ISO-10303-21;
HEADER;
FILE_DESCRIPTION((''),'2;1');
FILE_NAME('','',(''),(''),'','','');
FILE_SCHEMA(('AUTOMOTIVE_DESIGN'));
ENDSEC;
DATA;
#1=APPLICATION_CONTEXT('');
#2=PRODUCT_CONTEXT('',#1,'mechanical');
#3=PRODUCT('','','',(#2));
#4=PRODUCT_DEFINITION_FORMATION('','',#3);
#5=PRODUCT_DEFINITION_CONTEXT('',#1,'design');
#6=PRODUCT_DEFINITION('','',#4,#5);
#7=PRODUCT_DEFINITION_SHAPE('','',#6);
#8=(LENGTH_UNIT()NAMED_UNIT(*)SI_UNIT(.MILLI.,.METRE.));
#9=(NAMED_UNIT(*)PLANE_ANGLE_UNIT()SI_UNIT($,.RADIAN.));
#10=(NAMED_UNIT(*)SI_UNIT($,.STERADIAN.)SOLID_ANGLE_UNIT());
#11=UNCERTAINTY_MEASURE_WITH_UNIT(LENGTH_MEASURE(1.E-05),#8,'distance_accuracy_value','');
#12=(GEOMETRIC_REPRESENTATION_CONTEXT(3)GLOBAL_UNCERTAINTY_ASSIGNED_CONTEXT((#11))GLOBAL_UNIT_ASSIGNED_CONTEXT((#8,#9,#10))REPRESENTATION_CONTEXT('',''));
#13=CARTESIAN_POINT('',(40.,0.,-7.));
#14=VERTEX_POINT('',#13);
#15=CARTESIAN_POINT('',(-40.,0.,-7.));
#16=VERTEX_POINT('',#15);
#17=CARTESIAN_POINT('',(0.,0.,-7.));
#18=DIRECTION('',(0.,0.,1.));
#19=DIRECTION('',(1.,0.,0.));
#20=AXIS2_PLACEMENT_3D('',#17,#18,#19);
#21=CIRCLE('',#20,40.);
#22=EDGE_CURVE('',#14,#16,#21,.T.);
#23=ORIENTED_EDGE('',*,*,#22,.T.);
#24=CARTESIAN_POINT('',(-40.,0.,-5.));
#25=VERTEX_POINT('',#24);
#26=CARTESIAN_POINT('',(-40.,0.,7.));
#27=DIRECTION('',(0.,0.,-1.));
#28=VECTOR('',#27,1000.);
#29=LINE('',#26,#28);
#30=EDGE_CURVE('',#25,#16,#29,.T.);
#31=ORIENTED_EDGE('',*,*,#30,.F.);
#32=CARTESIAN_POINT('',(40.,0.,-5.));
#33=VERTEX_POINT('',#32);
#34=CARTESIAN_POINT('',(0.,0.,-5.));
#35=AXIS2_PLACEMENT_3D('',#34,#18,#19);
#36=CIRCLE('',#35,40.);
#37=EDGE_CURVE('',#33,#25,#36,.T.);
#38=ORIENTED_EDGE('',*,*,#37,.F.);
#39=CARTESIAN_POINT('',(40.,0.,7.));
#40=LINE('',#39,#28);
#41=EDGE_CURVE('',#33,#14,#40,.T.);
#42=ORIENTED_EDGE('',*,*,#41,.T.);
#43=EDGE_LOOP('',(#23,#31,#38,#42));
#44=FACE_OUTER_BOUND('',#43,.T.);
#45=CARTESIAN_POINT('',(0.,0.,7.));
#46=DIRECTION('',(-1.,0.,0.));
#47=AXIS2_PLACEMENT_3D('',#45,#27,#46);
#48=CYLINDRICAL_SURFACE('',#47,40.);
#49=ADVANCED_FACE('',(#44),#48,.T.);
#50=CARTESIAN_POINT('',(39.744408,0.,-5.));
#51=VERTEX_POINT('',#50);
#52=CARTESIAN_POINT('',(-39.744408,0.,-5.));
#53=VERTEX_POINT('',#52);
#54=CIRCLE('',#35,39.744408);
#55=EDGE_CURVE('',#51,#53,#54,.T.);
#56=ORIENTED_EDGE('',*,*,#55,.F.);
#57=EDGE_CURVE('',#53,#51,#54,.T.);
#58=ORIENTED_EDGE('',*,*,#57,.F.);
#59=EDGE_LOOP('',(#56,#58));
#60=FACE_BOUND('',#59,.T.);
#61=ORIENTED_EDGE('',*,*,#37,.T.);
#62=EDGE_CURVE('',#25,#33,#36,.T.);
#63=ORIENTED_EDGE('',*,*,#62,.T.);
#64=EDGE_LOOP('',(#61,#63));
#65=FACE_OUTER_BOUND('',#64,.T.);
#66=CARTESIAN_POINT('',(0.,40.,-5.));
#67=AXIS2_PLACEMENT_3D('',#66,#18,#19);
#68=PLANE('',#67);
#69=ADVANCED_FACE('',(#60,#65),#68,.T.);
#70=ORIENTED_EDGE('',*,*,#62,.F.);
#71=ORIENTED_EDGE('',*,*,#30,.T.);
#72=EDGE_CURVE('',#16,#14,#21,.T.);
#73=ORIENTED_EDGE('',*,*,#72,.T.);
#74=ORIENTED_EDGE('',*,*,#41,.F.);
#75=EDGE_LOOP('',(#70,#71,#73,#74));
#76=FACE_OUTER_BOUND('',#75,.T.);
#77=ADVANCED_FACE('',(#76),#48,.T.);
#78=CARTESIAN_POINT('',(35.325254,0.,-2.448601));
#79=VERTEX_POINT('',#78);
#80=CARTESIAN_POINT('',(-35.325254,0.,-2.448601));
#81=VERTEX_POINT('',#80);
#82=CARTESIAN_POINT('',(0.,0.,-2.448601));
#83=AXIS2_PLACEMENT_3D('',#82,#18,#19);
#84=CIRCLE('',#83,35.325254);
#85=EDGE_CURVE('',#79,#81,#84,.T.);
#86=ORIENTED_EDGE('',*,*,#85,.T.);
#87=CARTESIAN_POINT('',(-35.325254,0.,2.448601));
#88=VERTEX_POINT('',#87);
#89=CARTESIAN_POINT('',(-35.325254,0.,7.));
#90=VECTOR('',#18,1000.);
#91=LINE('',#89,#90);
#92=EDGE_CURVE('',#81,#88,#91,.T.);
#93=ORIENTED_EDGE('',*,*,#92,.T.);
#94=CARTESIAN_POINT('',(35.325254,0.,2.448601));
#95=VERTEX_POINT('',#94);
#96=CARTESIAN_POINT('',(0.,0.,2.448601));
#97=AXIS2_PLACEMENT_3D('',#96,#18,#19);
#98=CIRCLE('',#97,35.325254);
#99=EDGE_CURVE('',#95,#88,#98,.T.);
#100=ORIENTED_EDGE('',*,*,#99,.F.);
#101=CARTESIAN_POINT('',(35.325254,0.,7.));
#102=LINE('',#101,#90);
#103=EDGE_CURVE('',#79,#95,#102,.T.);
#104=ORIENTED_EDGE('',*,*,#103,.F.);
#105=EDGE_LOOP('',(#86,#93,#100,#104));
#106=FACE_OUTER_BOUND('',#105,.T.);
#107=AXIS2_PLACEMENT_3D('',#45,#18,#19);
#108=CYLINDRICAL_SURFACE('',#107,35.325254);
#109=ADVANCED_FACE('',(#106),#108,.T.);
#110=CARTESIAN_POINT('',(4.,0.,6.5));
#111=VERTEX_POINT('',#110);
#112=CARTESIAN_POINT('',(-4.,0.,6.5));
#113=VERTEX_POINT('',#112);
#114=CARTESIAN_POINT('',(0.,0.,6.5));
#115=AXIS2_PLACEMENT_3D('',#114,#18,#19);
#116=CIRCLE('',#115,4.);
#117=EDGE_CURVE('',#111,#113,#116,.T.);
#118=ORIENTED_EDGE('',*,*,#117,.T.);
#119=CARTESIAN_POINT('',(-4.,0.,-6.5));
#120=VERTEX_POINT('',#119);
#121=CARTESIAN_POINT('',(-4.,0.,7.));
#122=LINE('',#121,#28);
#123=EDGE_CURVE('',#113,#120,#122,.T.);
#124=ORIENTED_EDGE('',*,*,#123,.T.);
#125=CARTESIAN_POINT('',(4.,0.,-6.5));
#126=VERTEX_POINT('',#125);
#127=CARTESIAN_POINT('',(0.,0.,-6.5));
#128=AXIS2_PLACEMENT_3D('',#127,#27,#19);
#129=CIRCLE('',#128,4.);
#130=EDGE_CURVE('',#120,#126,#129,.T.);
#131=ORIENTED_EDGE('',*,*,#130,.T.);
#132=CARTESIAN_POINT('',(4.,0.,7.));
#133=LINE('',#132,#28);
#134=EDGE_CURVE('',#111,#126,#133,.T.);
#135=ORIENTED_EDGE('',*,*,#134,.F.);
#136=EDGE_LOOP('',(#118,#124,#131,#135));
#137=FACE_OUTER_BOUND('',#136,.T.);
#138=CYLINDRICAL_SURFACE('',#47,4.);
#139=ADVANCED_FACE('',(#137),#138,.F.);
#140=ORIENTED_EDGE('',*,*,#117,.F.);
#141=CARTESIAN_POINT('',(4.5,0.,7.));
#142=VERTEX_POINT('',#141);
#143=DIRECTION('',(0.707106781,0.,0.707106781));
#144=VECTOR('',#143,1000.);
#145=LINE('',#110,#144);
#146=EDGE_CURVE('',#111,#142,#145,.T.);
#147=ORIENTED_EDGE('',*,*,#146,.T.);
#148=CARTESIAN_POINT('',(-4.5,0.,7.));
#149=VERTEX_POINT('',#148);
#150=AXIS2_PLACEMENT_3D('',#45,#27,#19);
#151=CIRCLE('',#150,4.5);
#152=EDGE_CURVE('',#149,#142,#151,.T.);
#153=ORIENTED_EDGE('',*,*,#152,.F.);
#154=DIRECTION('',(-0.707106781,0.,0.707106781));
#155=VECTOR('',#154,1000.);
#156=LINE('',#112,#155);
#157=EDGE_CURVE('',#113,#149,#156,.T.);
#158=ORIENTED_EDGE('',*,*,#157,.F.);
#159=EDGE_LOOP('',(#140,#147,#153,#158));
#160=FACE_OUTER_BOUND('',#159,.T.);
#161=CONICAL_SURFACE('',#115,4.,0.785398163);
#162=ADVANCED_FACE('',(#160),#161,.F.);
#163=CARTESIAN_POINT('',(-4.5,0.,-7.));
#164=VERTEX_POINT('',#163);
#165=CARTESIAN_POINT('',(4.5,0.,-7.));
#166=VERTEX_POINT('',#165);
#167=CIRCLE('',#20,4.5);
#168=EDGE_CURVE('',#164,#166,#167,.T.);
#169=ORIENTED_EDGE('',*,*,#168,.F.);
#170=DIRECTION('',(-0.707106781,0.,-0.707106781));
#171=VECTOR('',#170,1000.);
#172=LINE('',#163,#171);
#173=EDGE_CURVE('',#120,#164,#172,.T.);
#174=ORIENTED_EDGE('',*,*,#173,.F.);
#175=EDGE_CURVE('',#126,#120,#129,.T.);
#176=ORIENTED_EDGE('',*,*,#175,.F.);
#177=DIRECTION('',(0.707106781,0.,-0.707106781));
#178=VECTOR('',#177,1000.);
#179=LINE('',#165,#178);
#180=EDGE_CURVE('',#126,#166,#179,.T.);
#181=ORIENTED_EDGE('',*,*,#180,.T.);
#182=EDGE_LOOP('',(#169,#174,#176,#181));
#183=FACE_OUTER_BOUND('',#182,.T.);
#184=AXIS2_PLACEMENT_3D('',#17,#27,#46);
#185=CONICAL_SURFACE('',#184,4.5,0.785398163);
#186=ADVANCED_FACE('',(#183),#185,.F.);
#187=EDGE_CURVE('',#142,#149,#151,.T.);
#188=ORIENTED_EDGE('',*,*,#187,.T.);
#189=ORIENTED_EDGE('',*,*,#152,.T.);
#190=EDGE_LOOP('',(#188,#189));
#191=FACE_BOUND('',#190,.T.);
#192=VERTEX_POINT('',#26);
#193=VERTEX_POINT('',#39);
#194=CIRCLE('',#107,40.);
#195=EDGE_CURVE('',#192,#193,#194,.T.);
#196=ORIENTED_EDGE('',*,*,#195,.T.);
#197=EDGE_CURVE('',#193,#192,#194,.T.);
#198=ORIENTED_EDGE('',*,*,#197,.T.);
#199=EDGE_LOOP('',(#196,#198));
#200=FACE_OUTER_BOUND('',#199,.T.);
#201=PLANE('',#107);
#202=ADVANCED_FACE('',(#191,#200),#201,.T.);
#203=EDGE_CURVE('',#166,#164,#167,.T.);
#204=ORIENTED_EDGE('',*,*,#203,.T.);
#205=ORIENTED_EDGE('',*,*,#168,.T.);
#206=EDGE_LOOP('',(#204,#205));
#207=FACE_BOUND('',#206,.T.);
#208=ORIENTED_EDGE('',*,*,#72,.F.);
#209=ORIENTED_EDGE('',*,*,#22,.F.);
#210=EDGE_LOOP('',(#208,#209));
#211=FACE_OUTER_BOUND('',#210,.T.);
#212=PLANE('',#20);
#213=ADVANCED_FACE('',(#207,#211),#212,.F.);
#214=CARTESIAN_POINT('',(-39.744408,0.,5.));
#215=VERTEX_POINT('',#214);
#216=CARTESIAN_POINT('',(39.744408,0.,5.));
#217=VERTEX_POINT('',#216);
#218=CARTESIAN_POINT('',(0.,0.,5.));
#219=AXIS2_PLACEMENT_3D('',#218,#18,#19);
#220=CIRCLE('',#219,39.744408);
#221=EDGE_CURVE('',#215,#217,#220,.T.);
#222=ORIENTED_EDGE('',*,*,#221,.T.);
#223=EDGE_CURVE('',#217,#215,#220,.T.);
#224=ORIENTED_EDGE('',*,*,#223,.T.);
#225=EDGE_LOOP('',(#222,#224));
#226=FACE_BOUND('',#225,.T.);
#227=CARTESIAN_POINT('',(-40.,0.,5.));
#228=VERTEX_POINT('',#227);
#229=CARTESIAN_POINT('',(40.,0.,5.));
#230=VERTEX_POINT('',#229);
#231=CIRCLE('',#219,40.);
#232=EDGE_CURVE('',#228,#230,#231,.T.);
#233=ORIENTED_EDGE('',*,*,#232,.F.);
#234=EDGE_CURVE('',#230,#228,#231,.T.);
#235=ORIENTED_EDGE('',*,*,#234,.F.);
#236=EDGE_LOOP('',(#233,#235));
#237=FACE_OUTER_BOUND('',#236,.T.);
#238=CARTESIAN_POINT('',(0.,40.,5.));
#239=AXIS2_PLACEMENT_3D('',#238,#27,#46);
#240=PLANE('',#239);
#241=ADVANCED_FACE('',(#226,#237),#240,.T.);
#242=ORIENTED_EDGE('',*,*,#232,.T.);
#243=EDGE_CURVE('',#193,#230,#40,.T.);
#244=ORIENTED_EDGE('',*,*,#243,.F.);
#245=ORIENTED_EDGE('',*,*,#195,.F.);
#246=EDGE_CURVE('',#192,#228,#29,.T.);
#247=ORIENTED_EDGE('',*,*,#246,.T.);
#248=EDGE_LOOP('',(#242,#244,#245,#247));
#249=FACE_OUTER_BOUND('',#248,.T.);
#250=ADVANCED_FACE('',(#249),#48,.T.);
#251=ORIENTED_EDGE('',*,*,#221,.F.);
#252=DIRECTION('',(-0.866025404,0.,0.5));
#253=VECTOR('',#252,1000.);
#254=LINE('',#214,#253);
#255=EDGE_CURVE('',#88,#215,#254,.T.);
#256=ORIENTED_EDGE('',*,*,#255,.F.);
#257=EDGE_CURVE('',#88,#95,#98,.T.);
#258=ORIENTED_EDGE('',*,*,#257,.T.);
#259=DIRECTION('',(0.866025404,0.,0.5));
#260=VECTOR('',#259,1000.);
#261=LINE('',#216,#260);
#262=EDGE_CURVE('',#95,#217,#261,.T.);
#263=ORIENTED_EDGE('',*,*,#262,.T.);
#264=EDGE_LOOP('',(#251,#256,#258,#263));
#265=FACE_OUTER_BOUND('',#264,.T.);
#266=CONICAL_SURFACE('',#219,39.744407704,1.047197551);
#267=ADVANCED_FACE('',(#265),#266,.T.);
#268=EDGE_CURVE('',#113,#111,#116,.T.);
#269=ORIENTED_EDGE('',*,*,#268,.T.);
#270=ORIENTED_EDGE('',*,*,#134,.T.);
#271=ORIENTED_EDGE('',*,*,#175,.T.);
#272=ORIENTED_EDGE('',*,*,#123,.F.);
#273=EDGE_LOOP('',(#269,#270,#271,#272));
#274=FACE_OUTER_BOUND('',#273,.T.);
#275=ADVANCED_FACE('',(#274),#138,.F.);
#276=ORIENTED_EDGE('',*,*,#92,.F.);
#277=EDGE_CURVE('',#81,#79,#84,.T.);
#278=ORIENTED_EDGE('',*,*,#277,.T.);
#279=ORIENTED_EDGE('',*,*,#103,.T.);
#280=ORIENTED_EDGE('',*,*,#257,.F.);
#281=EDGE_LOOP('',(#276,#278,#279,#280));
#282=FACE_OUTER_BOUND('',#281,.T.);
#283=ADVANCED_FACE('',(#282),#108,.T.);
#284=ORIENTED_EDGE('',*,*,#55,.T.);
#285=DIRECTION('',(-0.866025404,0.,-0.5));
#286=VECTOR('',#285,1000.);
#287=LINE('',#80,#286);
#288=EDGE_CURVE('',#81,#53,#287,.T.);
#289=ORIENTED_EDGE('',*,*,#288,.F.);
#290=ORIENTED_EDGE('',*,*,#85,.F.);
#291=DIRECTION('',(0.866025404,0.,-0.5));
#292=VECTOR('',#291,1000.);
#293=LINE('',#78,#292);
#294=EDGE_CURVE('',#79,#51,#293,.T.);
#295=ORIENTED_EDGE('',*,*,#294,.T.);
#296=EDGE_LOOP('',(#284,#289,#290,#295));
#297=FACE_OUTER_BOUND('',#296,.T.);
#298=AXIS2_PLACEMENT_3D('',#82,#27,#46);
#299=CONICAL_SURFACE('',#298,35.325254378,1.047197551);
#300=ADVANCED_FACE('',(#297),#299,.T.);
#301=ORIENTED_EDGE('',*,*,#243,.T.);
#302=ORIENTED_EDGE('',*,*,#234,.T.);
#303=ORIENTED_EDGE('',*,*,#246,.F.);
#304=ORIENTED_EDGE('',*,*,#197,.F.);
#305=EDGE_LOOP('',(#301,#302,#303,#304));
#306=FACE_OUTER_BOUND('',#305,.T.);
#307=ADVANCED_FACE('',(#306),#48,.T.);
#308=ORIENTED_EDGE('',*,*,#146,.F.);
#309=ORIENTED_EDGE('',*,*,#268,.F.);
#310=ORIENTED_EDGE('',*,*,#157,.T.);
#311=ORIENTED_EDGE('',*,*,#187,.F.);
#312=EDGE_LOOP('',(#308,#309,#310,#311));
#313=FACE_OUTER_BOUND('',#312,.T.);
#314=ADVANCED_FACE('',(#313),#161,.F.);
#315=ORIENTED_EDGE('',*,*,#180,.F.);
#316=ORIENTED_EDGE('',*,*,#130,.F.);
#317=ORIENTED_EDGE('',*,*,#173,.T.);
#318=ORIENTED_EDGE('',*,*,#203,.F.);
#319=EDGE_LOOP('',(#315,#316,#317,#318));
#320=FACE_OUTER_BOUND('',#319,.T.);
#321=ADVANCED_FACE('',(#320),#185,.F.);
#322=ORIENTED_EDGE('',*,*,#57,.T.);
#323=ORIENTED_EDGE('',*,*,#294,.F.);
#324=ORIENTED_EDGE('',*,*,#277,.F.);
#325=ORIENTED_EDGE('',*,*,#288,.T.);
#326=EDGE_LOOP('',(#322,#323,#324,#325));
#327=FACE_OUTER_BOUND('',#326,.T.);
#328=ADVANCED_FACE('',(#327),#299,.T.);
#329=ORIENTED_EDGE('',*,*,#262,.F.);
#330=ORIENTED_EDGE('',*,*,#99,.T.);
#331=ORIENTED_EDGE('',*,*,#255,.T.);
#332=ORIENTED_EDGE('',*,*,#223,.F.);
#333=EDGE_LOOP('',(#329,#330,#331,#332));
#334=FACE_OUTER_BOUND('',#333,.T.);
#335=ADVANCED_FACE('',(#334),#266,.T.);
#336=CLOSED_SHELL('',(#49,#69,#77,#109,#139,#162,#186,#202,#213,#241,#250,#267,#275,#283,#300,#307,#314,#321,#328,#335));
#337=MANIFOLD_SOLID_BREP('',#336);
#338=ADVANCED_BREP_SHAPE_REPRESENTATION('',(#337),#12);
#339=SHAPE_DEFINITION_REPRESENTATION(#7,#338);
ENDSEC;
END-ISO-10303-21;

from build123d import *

# Parameters (mm, degrees)
SKETCH1_R           = 40
SKETCH1_R_2         = 4
BOSS_EXTRUDE1_DEPTH = 7
CHAMFER1_SIZE       = 0.5


with BuildPart() as part:
    # Sketch1 → Boss-Extrude1 (new, symmetric)
    with BuildSketch(Plane.XY):
        Circle(SKETCH1_R)
        Circle(SKETCH1_R_2, mode=Mode.SUBTRACT)
    extrude(amount=BOSS_EXTRUDE1_DEPTH, both=True)

    # Sketch2 → Cut-Revolve1 (revolve, cut)
    with BuildSketch(Plane(origin=(0, 0, 0), x_dir=(0, 0, -1), z_dir=(1, 0, 0)), mode=Mode.PRIVATE) as cut_revolve1_sk:
        Polygon((-5, 39.744407704), (-2.448600638, 35.325254378), (2.448600638, 35.325254378), (5, 39.744407704), (5, 40), (-5, 40), align=None)
    revolve(cut_revolve1_sk.sketch.rotate(Axis((0, 0, 7), (0, 0, -1)), 90), axis=Axis((0, 0, 7), (0, 0, -1)), mode=Mode.SUBTRACT)

    # Chamfer1
    chamfer1_edges = [part.edges().sort_by_distance(p)[0] for p in [
        (-4, 0, -7),
        (-4, 0, 7),
    ]]
    chamfer(chamfer1_edges, length=CHAMFER1_SIZE)


solid = part.part
